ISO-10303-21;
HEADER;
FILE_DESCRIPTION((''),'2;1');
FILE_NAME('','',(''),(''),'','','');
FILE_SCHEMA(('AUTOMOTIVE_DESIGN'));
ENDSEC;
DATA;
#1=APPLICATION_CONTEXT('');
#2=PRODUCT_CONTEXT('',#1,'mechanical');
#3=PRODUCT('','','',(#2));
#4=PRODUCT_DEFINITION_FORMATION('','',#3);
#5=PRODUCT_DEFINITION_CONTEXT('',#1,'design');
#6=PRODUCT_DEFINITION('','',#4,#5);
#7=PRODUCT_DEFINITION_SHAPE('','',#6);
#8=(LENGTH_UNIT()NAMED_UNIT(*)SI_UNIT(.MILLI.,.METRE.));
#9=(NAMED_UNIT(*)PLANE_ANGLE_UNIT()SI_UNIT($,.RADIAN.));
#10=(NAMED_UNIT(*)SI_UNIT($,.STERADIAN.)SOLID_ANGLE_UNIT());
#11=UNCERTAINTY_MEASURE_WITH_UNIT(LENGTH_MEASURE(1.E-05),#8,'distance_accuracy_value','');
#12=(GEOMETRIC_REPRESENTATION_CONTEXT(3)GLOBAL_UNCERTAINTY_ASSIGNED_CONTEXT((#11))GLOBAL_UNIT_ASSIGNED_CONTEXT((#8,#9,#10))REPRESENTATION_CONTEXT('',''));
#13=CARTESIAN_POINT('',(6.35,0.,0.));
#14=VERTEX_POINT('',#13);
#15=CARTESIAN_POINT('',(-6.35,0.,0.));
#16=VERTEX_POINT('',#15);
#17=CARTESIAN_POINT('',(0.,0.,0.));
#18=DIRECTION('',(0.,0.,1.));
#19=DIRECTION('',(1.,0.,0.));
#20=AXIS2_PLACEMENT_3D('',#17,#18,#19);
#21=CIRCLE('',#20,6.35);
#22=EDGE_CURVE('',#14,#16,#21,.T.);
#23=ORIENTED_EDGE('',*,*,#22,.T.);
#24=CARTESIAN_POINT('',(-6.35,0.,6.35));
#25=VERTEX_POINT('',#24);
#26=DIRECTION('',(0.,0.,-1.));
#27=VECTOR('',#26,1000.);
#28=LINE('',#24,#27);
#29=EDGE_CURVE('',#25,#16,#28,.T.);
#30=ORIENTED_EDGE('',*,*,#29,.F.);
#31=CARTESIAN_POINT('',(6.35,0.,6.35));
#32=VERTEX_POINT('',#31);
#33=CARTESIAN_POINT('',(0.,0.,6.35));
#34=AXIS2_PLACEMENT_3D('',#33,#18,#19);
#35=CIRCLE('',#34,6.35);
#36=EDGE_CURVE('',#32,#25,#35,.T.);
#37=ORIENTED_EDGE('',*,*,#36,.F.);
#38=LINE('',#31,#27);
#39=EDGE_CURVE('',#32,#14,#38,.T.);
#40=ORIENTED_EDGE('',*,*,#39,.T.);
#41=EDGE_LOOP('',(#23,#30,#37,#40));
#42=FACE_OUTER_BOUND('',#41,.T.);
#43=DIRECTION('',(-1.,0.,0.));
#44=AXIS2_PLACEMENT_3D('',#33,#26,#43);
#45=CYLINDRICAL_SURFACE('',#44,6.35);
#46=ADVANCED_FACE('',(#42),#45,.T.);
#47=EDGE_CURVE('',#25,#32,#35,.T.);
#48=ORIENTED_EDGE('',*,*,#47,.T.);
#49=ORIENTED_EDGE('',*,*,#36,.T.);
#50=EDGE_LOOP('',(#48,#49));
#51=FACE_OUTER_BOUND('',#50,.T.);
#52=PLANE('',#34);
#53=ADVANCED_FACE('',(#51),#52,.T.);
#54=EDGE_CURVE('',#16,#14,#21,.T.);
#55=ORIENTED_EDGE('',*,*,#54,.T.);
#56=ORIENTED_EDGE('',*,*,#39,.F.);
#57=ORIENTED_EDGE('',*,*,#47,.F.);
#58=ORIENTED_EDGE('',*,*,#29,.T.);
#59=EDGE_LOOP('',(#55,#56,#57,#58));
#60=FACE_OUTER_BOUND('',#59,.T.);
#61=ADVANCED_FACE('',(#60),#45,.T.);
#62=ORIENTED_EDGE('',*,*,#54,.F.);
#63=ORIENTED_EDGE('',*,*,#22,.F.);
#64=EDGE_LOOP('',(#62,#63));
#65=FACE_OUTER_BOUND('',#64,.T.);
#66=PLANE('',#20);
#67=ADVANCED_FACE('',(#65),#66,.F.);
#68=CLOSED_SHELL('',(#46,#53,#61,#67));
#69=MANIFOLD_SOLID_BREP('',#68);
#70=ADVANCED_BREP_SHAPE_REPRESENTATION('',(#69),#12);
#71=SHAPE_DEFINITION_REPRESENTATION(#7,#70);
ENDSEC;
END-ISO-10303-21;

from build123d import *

# Parameters (mm, degrees)
SKETCH1_R           = 6.35
BOSS_EXTRUDE1_DEPTH = 6.35


with BuildPart() as part:
    # Sketch1 → Boss-Extrude1 (new body)
    with BuildSketch(Plane.XY):
        Circle(SKETCH1_R)
    extrude(amount=BOSS_EXTRUDE1_DEPTH)


solid = part.part
